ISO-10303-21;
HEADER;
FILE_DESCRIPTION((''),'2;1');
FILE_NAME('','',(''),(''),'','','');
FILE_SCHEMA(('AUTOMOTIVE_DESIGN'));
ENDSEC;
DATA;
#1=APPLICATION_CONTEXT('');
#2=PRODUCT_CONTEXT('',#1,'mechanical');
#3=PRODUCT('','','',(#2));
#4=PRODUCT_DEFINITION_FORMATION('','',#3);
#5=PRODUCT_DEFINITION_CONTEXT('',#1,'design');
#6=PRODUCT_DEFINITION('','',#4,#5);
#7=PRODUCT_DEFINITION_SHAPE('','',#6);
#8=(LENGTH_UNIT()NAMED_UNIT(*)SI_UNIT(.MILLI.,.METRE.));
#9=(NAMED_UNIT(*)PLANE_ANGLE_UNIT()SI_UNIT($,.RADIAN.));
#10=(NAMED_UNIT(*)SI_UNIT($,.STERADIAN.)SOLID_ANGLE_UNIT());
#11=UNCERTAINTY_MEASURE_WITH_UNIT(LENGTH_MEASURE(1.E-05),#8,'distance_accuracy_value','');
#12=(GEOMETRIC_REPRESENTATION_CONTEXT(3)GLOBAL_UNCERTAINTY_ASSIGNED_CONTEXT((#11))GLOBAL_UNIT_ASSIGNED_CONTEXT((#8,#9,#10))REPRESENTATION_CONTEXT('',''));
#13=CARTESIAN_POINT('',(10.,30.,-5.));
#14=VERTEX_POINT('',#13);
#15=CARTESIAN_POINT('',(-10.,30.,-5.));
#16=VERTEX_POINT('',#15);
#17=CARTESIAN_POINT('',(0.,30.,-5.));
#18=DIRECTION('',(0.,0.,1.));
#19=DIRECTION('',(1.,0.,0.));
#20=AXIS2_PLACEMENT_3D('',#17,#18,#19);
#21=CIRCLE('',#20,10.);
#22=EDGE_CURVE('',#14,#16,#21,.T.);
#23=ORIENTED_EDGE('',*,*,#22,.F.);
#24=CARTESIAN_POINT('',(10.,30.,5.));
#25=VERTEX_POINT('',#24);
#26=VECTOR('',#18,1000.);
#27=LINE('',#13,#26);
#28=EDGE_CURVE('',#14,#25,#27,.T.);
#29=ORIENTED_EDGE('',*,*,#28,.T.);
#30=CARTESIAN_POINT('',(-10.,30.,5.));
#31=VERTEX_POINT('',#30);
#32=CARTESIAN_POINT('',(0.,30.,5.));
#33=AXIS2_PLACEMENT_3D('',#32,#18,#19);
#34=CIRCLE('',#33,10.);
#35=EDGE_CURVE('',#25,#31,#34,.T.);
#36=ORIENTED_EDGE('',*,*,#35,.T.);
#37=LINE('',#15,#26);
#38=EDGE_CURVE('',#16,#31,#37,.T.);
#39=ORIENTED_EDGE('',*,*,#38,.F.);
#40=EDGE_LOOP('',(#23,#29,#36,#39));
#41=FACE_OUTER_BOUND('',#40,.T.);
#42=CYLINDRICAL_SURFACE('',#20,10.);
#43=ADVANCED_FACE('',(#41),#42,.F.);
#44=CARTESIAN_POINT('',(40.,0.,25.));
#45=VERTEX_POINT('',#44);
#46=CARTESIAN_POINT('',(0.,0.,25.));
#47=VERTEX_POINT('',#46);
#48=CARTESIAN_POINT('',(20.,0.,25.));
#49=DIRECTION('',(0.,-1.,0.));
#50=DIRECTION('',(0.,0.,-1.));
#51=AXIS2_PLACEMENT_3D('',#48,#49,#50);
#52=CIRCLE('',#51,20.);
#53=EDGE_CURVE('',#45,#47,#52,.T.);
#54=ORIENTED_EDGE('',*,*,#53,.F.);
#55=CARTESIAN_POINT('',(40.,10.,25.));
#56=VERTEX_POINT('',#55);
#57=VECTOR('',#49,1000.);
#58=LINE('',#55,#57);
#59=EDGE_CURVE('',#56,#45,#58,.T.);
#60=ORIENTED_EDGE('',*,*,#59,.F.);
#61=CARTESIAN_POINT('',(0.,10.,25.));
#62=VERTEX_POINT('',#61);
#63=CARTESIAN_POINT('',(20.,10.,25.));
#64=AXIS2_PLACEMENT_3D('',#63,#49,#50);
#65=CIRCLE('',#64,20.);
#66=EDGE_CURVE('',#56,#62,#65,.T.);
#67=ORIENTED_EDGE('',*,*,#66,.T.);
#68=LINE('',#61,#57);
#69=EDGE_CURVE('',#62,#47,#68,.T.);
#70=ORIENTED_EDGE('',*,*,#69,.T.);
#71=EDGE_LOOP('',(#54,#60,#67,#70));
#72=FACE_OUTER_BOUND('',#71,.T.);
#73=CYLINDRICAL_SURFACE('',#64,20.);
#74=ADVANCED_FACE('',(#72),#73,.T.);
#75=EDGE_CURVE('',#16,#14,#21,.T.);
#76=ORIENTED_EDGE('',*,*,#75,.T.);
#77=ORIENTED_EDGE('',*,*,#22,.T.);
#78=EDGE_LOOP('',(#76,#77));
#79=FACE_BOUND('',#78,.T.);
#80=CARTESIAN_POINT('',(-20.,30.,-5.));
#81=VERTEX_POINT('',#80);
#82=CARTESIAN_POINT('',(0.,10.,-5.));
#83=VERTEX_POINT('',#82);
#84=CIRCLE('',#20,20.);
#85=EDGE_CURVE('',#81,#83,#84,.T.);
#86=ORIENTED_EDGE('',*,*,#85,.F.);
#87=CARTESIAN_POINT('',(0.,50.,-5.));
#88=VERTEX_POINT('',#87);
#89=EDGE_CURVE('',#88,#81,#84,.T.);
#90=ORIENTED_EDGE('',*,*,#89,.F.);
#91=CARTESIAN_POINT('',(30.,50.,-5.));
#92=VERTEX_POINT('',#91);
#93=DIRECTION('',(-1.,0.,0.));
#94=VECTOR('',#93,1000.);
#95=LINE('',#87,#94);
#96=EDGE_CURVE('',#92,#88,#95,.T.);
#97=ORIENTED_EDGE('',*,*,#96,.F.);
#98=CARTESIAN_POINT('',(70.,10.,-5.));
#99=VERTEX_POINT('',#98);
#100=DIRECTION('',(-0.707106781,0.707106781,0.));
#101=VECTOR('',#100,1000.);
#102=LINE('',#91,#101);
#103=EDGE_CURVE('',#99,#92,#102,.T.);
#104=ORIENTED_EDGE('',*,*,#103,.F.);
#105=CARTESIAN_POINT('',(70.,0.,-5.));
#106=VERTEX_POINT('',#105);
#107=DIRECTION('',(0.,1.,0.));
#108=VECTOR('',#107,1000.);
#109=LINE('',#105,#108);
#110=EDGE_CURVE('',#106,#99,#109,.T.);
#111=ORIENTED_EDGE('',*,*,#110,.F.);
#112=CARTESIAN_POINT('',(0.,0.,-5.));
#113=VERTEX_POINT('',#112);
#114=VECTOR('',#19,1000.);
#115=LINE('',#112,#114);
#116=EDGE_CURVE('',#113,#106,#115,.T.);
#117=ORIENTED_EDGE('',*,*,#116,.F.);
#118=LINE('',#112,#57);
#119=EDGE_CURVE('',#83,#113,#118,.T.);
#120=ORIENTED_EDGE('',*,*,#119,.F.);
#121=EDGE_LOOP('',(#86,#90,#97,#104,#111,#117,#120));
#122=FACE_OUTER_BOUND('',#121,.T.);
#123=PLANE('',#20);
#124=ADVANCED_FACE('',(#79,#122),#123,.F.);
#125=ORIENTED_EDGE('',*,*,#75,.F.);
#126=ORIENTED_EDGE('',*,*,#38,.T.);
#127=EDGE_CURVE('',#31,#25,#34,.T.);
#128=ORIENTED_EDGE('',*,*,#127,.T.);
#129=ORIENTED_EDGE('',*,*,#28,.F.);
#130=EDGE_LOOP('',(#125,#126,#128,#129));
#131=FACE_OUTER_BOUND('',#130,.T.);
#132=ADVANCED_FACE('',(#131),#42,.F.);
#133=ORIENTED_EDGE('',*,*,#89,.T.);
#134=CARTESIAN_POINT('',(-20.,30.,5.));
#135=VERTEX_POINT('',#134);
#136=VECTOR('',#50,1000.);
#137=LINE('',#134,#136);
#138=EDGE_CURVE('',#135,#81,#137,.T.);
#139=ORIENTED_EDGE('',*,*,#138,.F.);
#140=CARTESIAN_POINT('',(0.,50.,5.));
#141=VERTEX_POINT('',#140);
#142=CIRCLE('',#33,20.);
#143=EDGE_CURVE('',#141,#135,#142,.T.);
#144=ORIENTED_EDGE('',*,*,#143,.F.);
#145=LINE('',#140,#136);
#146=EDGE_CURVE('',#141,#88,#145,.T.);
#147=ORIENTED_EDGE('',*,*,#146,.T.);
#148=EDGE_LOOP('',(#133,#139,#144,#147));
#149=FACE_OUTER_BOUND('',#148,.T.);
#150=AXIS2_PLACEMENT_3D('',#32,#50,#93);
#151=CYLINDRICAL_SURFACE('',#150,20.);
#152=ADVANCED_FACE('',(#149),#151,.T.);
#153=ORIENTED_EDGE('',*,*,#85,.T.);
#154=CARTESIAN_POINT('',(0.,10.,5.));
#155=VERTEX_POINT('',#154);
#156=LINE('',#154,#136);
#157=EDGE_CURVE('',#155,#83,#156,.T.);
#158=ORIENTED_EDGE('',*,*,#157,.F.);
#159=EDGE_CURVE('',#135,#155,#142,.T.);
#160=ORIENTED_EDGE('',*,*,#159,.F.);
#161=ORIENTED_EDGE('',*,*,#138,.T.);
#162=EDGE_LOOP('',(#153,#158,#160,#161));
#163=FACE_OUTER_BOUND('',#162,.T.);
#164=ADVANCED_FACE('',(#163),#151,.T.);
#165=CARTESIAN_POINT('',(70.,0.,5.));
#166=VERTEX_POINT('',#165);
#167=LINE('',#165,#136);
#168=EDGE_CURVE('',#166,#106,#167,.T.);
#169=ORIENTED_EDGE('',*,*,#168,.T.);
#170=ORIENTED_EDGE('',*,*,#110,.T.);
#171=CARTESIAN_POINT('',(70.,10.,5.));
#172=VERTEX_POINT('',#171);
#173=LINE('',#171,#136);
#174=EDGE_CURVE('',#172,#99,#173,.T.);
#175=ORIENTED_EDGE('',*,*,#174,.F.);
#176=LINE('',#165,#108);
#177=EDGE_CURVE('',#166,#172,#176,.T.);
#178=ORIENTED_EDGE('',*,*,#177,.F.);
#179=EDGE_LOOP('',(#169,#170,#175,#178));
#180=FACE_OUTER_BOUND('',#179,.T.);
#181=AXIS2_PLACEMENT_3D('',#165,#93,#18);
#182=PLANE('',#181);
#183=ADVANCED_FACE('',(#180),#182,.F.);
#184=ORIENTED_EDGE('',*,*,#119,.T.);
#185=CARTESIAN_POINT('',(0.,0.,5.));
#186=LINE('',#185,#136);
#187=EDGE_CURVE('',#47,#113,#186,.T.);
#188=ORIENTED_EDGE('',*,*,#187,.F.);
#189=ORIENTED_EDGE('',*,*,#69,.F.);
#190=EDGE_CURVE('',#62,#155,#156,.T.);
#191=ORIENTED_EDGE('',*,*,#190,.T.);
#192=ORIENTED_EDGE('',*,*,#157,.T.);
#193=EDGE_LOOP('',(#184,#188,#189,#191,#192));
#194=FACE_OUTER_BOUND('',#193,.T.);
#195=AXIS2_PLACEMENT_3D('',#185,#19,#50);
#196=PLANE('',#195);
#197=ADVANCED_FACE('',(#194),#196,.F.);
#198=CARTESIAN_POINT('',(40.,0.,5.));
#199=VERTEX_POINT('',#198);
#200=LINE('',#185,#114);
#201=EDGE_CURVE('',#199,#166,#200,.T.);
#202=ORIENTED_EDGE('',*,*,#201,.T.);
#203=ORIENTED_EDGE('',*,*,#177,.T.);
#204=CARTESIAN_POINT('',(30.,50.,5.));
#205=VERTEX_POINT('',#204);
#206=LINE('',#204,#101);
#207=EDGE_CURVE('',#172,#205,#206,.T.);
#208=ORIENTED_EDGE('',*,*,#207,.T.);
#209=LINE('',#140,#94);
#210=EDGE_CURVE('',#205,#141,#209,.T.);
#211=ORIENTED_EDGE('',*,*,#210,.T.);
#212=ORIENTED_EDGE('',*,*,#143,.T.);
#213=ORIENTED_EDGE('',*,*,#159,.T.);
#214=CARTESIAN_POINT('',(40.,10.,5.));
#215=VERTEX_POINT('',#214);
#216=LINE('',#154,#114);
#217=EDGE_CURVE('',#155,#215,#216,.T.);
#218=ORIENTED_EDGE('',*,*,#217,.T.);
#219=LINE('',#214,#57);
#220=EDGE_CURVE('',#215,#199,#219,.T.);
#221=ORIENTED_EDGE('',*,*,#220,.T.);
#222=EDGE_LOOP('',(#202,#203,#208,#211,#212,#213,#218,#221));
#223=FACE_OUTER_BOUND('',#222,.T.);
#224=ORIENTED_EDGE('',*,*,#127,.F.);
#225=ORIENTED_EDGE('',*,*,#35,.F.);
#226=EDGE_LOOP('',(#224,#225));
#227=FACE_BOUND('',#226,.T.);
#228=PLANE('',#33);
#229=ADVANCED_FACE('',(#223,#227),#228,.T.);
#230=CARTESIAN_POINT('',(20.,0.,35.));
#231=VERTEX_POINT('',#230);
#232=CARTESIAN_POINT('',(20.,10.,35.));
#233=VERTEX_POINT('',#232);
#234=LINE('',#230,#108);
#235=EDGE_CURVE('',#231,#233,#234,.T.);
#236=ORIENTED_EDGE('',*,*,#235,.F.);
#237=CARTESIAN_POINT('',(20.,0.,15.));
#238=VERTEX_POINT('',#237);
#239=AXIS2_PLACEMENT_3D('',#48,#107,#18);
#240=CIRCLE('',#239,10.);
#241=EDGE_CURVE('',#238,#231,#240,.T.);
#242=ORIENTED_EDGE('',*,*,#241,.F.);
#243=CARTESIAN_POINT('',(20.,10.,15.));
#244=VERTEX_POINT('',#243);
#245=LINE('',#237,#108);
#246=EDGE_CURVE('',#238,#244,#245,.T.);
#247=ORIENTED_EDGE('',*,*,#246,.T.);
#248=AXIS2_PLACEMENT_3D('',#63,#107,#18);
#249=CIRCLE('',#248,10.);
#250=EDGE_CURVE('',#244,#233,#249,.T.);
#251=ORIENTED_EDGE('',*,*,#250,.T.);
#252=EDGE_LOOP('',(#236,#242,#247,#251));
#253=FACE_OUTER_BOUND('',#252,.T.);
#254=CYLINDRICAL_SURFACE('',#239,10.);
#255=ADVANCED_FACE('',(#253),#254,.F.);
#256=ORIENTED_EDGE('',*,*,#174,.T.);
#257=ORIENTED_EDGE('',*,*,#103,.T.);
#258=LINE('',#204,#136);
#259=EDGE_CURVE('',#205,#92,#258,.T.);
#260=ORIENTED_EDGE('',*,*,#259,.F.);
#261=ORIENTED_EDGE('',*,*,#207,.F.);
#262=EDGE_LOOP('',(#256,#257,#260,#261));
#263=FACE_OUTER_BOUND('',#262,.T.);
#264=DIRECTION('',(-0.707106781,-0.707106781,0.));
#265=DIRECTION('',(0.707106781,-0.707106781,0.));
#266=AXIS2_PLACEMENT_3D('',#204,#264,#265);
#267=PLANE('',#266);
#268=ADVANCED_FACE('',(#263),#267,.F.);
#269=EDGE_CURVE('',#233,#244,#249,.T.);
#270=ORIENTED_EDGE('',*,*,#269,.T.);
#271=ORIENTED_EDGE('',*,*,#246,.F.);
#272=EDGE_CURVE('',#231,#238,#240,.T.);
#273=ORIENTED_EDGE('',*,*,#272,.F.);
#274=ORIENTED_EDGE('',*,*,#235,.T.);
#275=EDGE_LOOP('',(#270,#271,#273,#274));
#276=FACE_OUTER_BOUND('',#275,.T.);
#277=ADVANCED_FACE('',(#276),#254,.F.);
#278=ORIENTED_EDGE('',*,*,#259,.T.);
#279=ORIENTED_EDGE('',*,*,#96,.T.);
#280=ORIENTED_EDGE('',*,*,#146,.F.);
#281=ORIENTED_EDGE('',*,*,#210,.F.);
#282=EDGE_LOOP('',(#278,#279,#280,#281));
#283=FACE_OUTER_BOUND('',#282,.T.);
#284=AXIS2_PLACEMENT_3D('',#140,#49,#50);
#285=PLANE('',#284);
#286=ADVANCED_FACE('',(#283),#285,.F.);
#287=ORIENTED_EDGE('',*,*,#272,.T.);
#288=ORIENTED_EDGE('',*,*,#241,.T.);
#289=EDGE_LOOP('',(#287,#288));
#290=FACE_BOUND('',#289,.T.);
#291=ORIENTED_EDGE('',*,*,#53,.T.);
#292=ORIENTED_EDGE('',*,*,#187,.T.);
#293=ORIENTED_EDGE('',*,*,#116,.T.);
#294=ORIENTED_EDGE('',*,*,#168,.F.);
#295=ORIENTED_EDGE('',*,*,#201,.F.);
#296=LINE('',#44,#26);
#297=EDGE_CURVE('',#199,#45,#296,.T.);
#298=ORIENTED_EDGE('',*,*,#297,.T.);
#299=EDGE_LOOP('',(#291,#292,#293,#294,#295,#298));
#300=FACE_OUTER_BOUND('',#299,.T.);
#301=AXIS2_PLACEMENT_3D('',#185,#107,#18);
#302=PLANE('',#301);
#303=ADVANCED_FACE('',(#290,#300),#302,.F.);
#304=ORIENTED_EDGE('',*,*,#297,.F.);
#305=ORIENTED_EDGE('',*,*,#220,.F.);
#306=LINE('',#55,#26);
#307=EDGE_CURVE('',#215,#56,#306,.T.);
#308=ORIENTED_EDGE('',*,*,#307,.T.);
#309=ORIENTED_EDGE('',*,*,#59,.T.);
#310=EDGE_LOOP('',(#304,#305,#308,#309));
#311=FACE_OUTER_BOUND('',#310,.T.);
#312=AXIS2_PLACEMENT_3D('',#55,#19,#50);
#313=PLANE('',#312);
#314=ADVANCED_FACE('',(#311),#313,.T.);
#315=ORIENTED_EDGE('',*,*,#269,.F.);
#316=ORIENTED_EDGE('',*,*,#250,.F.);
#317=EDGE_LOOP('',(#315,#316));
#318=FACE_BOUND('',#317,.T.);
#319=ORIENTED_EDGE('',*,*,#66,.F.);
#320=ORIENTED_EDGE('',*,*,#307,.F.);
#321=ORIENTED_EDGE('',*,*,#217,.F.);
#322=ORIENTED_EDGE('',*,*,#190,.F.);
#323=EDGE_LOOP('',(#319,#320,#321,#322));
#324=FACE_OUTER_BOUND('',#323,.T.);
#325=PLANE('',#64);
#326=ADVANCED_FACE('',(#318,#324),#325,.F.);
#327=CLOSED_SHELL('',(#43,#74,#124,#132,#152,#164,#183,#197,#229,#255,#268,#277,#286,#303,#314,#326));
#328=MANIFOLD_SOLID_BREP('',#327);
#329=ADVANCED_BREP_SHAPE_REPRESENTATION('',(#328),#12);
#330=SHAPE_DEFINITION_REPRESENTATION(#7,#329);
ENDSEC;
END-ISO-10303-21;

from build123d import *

# Parameters (mm, degrees)
UPRIGHT_PLATE_DEPTH          = 5
BASE_LUG_DEPTH               = 10
BASE_LUG_HOLE_PROFILE_R      = 10
BASE_LUG_HOLE_20_DEPTH       = 93.330926563
UPRIGHT_PLATE_HOLE_PROFILE_R = 10
UPRIGHT_PLATE_HOLE_20_DEPTH  = 95.868329805


with BuildPart() as part:
    # Upright Plate Profile → Upright Plate (new, symmetric)
    with BuildSketch(Plane.XY):
        with BuildLine():
            Line((0, 50), (30, 50))
            Line((30, 50), (70, 10))
            Line((70, 10), (70, 0))
            Line((70, 0), (0, 0))
            Line((0, 0), (0, 10))
            ThreePointArc((0, 10), (-20, 30), (0, 50))
        make_face()
    extrude(amount=UPRIGHT_PLATE_DEPTH, both=True)

    # Base Lug Profile → Base Lug (add)
    with BuildSketch(Plane.XZ):
        with BuildLine():
            Line((0, 5), (0, 25))
            ThreePointArc((0, 25), (20, 45), (40, 25))
            Line((40, 25), (40, 5))
            Line((40, 5), (70, 5))
            Line((70, 5), (70, -5))
            Line((70, -5), (0, -5))
            Line((0, -5), (0, 5))
        make_face()
    extrude(amount=-BASE_LUG_DEPTH)

    # Base Lug Hole Profile → Base Lug Hole Ø20 (cut, through all)
    with BuildSketch(Plane(origin=(0, 10, 0), x_dir=(1, 0, 0), z_dir=(0, 1, 0))):
        with Locations(Location((20, -25, 0), (0, 0, 270))):
            Circle(BASE_LUG_HOLE_PROFILE_R)
    extrude(amount=-BASE_LUG_HOLE_20_DEPTH, mode=Mode.SUBTRACT)

    # Upright Plate Hole Profile → Upright Plate Hole Ø20 (cut, through all)
    with BuildSketch(Plane.XY.offset(5)):
        with Locations((0, 30)):
            Circle(UPRIGHT_PLATE_HOLE_PROFILE_R)
    extrude(amount=-UPRIGHT_PLATE_HOLE_20_DEPTH, mode=Mode.SUBTRACT)


solid = part.part
